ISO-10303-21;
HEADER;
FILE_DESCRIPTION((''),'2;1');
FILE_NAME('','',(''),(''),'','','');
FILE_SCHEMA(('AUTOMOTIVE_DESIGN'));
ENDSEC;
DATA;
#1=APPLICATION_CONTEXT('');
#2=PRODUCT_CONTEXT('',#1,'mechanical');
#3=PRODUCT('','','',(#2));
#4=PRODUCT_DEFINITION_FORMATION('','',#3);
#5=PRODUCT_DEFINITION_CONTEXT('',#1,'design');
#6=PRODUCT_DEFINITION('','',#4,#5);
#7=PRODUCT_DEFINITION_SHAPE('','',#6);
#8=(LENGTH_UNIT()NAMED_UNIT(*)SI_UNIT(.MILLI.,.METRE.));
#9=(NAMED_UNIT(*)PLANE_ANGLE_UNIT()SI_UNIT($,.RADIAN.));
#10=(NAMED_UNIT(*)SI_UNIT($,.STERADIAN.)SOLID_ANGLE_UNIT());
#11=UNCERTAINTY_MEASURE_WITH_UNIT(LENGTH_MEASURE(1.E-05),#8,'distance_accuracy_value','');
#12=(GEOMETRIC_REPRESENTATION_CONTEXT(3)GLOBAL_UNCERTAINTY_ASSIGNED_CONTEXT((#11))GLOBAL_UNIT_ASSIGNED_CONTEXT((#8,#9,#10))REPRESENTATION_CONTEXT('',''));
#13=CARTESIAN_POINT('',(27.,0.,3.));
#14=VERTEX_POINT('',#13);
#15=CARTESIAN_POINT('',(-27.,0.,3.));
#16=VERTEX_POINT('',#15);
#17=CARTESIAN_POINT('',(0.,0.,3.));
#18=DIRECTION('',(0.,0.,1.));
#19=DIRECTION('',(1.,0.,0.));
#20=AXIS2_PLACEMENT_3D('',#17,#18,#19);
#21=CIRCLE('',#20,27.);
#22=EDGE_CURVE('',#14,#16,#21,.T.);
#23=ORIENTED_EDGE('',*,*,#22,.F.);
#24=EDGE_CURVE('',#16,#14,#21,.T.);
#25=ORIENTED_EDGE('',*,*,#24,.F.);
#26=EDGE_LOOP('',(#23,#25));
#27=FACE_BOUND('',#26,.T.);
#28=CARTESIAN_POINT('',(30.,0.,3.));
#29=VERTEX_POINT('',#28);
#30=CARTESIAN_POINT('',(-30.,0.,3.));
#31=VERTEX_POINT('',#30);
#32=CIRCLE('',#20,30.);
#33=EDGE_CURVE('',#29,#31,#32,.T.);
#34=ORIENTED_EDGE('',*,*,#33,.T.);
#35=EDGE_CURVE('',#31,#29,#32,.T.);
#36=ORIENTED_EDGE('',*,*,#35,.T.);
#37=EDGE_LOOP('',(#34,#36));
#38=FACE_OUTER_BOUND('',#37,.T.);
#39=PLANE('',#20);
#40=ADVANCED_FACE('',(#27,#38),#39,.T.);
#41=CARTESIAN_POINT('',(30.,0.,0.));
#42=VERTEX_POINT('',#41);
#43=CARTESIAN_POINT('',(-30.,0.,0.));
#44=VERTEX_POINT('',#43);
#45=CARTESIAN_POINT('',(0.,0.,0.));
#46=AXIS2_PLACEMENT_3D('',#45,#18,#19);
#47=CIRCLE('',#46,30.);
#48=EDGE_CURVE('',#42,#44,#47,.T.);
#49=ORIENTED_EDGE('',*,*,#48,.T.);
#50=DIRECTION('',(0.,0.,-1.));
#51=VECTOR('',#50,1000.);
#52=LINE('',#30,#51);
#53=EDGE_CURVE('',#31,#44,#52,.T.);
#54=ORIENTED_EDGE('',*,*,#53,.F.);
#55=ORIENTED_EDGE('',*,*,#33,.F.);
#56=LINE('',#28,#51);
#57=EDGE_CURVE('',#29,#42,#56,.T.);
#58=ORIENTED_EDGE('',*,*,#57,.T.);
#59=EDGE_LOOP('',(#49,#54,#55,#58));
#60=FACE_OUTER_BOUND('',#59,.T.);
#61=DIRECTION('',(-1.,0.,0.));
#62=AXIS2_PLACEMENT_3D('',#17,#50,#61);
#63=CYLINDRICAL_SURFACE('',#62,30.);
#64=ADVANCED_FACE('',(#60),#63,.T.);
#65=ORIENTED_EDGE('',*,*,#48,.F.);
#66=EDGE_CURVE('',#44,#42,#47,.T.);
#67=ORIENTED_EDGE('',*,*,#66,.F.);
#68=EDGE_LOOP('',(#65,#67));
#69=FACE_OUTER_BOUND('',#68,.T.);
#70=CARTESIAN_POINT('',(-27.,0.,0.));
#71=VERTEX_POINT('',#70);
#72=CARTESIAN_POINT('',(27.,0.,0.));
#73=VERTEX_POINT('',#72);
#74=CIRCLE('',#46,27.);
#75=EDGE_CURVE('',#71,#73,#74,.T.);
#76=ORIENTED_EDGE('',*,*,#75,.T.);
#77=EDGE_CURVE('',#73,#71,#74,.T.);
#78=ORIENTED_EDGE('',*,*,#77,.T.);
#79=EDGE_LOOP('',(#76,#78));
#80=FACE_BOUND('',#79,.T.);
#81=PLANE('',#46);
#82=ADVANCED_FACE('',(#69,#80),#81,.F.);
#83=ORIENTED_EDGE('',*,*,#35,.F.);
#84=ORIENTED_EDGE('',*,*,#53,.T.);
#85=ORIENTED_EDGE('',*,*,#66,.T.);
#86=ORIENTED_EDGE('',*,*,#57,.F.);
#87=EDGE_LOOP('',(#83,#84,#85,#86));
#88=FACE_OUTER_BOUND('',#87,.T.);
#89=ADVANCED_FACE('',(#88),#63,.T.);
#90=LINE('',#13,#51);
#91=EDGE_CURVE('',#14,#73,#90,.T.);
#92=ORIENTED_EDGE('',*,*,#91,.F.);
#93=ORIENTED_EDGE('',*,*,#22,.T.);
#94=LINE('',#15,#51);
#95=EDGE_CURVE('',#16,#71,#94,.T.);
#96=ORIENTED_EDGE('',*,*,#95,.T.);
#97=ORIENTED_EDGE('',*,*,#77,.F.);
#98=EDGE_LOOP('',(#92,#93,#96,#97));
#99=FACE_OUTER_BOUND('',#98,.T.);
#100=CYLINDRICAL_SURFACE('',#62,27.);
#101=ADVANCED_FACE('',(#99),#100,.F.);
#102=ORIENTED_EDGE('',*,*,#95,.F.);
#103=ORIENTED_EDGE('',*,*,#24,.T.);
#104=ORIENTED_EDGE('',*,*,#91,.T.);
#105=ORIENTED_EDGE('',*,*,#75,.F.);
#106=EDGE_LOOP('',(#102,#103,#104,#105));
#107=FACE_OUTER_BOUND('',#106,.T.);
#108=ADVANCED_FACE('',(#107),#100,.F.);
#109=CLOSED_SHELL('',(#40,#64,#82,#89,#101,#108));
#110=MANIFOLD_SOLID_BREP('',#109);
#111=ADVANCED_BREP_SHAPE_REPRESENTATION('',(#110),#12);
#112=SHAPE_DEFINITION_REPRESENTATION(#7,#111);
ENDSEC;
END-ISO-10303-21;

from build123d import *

# Parameters (mm, degrees)
SKETCH_1_R      = 30
SKETCH_1_R_2    = 27
EXTRUDE_1_DEPTH = 3


with BuildPart() as part:
    # 草图1 → 凸台-拉伸1 (new body)
    with BuildSketch(Plane.XY):
        Circle(SKETCH_1_R)
        Circle(SKETCH_1_R_2, mode=Mode.SUBTRACT)
    extrude(amount=EXTRUDE_1_DEPTH)


solid = part.part
